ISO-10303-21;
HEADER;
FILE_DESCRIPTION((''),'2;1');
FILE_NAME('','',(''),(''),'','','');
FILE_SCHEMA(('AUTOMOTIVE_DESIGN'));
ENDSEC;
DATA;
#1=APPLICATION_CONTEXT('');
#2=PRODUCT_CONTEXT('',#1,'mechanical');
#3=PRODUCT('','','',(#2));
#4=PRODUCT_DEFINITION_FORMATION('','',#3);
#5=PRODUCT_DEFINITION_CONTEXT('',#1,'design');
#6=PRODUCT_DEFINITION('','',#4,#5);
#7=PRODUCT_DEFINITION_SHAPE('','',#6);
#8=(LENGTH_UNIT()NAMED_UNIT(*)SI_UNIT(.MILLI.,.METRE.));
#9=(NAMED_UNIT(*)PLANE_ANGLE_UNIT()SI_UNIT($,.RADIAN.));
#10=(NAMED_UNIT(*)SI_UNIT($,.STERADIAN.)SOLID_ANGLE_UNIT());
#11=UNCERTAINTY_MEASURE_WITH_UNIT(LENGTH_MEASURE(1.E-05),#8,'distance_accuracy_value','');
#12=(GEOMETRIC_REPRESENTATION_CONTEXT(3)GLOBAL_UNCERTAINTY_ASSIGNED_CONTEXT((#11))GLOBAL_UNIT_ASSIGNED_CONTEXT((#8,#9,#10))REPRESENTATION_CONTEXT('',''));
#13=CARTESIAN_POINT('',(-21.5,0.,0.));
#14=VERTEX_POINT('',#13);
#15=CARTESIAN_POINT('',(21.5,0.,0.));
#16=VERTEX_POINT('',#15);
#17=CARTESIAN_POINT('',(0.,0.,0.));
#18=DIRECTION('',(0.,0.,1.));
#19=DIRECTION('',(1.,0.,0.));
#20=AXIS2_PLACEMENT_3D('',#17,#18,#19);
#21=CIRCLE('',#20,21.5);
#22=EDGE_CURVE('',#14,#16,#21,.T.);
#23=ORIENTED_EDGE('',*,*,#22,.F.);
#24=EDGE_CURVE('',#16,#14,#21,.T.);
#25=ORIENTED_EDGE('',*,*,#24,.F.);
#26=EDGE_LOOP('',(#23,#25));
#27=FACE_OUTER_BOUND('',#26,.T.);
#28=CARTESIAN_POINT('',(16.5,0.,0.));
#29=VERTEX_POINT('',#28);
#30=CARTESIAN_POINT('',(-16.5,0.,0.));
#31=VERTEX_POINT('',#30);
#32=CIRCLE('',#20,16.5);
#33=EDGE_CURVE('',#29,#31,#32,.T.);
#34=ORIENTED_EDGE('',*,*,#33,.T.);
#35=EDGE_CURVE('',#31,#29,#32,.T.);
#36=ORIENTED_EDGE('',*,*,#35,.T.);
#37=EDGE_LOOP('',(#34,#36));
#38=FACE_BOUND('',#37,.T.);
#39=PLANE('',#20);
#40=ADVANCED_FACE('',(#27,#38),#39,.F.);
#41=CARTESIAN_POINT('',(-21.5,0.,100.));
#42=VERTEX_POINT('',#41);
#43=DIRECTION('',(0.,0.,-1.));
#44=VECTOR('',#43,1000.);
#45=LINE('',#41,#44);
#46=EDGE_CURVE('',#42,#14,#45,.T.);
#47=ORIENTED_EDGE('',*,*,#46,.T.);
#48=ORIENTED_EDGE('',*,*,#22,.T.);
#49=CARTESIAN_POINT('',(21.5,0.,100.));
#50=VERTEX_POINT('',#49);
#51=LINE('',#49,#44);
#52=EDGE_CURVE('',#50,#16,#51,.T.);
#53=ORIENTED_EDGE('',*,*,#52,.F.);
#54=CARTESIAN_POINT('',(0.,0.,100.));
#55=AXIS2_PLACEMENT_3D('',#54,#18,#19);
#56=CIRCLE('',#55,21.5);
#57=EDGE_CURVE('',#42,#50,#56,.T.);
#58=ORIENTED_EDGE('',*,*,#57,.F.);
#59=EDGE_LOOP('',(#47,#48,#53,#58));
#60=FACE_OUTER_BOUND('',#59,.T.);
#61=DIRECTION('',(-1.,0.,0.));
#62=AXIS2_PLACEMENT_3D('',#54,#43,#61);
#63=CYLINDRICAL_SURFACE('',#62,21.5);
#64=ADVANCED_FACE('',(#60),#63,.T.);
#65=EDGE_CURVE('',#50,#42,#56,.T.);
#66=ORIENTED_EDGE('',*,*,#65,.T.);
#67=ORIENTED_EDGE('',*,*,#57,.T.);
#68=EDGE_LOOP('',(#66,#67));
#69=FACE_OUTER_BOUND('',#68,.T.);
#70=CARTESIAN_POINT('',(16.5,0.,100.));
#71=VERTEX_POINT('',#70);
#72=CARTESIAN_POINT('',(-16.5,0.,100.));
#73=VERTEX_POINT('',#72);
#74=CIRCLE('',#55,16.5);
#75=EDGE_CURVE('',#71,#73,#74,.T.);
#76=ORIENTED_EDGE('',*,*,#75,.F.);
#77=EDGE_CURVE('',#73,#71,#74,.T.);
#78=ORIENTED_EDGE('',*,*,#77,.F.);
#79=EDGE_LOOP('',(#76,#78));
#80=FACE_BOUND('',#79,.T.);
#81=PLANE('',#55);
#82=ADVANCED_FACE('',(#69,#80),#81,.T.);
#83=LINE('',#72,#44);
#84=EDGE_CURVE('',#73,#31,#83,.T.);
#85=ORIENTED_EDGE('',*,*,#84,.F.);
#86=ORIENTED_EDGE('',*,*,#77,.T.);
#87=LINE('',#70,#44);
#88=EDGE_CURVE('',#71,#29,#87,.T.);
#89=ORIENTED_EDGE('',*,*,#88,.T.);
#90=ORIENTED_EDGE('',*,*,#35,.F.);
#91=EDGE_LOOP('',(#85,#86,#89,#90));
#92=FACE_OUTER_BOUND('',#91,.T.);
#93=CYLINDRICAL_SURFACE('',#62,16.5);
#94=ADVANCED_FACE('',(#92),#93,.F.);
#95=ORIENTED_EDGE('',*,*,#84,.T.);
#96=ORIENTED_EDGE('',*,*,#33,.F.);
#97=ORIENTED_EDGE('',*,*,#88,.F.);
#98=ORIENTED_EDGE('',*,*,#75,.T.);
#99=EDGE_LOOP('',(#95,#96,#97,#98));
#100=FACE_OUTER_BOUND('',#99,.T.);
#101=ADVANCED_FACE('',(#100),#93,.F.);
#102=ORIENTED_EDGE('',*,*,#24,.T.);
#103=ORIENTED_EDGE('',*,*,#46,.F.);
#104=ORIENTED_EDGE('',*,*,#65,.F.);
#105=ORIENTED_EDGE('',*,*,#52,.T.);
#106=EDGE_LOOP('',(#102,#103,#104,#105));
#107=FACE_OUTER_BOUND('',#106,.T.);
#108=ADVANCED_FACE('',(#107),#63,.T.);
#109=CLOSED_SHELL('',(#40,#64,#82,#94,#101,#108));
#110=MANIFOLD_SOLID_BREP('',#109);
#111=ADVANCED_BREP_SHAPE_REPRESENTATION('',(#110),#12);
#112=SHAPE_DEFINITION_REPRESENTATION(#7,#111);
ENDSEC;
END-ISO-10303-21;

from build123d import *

# Parameters (mm, degrees)
SKETCH_1_R      = 21.5
SKETCH_1_R_2    = 16.5
EXTRUDE_1_DEPTH = 100


with BuildPart() as part:
    # 草图1 → 凸台-拉伸1 (new body)
    with BuildSketch(Plane.XY):
        Circle(SKETCH_1_R)
        Circle(SKETCH_1_R_2, mode=Mode.SUBTRACT)
    extrude(amount=EXTRUDE_1_DEPTH)


solid = part.part
